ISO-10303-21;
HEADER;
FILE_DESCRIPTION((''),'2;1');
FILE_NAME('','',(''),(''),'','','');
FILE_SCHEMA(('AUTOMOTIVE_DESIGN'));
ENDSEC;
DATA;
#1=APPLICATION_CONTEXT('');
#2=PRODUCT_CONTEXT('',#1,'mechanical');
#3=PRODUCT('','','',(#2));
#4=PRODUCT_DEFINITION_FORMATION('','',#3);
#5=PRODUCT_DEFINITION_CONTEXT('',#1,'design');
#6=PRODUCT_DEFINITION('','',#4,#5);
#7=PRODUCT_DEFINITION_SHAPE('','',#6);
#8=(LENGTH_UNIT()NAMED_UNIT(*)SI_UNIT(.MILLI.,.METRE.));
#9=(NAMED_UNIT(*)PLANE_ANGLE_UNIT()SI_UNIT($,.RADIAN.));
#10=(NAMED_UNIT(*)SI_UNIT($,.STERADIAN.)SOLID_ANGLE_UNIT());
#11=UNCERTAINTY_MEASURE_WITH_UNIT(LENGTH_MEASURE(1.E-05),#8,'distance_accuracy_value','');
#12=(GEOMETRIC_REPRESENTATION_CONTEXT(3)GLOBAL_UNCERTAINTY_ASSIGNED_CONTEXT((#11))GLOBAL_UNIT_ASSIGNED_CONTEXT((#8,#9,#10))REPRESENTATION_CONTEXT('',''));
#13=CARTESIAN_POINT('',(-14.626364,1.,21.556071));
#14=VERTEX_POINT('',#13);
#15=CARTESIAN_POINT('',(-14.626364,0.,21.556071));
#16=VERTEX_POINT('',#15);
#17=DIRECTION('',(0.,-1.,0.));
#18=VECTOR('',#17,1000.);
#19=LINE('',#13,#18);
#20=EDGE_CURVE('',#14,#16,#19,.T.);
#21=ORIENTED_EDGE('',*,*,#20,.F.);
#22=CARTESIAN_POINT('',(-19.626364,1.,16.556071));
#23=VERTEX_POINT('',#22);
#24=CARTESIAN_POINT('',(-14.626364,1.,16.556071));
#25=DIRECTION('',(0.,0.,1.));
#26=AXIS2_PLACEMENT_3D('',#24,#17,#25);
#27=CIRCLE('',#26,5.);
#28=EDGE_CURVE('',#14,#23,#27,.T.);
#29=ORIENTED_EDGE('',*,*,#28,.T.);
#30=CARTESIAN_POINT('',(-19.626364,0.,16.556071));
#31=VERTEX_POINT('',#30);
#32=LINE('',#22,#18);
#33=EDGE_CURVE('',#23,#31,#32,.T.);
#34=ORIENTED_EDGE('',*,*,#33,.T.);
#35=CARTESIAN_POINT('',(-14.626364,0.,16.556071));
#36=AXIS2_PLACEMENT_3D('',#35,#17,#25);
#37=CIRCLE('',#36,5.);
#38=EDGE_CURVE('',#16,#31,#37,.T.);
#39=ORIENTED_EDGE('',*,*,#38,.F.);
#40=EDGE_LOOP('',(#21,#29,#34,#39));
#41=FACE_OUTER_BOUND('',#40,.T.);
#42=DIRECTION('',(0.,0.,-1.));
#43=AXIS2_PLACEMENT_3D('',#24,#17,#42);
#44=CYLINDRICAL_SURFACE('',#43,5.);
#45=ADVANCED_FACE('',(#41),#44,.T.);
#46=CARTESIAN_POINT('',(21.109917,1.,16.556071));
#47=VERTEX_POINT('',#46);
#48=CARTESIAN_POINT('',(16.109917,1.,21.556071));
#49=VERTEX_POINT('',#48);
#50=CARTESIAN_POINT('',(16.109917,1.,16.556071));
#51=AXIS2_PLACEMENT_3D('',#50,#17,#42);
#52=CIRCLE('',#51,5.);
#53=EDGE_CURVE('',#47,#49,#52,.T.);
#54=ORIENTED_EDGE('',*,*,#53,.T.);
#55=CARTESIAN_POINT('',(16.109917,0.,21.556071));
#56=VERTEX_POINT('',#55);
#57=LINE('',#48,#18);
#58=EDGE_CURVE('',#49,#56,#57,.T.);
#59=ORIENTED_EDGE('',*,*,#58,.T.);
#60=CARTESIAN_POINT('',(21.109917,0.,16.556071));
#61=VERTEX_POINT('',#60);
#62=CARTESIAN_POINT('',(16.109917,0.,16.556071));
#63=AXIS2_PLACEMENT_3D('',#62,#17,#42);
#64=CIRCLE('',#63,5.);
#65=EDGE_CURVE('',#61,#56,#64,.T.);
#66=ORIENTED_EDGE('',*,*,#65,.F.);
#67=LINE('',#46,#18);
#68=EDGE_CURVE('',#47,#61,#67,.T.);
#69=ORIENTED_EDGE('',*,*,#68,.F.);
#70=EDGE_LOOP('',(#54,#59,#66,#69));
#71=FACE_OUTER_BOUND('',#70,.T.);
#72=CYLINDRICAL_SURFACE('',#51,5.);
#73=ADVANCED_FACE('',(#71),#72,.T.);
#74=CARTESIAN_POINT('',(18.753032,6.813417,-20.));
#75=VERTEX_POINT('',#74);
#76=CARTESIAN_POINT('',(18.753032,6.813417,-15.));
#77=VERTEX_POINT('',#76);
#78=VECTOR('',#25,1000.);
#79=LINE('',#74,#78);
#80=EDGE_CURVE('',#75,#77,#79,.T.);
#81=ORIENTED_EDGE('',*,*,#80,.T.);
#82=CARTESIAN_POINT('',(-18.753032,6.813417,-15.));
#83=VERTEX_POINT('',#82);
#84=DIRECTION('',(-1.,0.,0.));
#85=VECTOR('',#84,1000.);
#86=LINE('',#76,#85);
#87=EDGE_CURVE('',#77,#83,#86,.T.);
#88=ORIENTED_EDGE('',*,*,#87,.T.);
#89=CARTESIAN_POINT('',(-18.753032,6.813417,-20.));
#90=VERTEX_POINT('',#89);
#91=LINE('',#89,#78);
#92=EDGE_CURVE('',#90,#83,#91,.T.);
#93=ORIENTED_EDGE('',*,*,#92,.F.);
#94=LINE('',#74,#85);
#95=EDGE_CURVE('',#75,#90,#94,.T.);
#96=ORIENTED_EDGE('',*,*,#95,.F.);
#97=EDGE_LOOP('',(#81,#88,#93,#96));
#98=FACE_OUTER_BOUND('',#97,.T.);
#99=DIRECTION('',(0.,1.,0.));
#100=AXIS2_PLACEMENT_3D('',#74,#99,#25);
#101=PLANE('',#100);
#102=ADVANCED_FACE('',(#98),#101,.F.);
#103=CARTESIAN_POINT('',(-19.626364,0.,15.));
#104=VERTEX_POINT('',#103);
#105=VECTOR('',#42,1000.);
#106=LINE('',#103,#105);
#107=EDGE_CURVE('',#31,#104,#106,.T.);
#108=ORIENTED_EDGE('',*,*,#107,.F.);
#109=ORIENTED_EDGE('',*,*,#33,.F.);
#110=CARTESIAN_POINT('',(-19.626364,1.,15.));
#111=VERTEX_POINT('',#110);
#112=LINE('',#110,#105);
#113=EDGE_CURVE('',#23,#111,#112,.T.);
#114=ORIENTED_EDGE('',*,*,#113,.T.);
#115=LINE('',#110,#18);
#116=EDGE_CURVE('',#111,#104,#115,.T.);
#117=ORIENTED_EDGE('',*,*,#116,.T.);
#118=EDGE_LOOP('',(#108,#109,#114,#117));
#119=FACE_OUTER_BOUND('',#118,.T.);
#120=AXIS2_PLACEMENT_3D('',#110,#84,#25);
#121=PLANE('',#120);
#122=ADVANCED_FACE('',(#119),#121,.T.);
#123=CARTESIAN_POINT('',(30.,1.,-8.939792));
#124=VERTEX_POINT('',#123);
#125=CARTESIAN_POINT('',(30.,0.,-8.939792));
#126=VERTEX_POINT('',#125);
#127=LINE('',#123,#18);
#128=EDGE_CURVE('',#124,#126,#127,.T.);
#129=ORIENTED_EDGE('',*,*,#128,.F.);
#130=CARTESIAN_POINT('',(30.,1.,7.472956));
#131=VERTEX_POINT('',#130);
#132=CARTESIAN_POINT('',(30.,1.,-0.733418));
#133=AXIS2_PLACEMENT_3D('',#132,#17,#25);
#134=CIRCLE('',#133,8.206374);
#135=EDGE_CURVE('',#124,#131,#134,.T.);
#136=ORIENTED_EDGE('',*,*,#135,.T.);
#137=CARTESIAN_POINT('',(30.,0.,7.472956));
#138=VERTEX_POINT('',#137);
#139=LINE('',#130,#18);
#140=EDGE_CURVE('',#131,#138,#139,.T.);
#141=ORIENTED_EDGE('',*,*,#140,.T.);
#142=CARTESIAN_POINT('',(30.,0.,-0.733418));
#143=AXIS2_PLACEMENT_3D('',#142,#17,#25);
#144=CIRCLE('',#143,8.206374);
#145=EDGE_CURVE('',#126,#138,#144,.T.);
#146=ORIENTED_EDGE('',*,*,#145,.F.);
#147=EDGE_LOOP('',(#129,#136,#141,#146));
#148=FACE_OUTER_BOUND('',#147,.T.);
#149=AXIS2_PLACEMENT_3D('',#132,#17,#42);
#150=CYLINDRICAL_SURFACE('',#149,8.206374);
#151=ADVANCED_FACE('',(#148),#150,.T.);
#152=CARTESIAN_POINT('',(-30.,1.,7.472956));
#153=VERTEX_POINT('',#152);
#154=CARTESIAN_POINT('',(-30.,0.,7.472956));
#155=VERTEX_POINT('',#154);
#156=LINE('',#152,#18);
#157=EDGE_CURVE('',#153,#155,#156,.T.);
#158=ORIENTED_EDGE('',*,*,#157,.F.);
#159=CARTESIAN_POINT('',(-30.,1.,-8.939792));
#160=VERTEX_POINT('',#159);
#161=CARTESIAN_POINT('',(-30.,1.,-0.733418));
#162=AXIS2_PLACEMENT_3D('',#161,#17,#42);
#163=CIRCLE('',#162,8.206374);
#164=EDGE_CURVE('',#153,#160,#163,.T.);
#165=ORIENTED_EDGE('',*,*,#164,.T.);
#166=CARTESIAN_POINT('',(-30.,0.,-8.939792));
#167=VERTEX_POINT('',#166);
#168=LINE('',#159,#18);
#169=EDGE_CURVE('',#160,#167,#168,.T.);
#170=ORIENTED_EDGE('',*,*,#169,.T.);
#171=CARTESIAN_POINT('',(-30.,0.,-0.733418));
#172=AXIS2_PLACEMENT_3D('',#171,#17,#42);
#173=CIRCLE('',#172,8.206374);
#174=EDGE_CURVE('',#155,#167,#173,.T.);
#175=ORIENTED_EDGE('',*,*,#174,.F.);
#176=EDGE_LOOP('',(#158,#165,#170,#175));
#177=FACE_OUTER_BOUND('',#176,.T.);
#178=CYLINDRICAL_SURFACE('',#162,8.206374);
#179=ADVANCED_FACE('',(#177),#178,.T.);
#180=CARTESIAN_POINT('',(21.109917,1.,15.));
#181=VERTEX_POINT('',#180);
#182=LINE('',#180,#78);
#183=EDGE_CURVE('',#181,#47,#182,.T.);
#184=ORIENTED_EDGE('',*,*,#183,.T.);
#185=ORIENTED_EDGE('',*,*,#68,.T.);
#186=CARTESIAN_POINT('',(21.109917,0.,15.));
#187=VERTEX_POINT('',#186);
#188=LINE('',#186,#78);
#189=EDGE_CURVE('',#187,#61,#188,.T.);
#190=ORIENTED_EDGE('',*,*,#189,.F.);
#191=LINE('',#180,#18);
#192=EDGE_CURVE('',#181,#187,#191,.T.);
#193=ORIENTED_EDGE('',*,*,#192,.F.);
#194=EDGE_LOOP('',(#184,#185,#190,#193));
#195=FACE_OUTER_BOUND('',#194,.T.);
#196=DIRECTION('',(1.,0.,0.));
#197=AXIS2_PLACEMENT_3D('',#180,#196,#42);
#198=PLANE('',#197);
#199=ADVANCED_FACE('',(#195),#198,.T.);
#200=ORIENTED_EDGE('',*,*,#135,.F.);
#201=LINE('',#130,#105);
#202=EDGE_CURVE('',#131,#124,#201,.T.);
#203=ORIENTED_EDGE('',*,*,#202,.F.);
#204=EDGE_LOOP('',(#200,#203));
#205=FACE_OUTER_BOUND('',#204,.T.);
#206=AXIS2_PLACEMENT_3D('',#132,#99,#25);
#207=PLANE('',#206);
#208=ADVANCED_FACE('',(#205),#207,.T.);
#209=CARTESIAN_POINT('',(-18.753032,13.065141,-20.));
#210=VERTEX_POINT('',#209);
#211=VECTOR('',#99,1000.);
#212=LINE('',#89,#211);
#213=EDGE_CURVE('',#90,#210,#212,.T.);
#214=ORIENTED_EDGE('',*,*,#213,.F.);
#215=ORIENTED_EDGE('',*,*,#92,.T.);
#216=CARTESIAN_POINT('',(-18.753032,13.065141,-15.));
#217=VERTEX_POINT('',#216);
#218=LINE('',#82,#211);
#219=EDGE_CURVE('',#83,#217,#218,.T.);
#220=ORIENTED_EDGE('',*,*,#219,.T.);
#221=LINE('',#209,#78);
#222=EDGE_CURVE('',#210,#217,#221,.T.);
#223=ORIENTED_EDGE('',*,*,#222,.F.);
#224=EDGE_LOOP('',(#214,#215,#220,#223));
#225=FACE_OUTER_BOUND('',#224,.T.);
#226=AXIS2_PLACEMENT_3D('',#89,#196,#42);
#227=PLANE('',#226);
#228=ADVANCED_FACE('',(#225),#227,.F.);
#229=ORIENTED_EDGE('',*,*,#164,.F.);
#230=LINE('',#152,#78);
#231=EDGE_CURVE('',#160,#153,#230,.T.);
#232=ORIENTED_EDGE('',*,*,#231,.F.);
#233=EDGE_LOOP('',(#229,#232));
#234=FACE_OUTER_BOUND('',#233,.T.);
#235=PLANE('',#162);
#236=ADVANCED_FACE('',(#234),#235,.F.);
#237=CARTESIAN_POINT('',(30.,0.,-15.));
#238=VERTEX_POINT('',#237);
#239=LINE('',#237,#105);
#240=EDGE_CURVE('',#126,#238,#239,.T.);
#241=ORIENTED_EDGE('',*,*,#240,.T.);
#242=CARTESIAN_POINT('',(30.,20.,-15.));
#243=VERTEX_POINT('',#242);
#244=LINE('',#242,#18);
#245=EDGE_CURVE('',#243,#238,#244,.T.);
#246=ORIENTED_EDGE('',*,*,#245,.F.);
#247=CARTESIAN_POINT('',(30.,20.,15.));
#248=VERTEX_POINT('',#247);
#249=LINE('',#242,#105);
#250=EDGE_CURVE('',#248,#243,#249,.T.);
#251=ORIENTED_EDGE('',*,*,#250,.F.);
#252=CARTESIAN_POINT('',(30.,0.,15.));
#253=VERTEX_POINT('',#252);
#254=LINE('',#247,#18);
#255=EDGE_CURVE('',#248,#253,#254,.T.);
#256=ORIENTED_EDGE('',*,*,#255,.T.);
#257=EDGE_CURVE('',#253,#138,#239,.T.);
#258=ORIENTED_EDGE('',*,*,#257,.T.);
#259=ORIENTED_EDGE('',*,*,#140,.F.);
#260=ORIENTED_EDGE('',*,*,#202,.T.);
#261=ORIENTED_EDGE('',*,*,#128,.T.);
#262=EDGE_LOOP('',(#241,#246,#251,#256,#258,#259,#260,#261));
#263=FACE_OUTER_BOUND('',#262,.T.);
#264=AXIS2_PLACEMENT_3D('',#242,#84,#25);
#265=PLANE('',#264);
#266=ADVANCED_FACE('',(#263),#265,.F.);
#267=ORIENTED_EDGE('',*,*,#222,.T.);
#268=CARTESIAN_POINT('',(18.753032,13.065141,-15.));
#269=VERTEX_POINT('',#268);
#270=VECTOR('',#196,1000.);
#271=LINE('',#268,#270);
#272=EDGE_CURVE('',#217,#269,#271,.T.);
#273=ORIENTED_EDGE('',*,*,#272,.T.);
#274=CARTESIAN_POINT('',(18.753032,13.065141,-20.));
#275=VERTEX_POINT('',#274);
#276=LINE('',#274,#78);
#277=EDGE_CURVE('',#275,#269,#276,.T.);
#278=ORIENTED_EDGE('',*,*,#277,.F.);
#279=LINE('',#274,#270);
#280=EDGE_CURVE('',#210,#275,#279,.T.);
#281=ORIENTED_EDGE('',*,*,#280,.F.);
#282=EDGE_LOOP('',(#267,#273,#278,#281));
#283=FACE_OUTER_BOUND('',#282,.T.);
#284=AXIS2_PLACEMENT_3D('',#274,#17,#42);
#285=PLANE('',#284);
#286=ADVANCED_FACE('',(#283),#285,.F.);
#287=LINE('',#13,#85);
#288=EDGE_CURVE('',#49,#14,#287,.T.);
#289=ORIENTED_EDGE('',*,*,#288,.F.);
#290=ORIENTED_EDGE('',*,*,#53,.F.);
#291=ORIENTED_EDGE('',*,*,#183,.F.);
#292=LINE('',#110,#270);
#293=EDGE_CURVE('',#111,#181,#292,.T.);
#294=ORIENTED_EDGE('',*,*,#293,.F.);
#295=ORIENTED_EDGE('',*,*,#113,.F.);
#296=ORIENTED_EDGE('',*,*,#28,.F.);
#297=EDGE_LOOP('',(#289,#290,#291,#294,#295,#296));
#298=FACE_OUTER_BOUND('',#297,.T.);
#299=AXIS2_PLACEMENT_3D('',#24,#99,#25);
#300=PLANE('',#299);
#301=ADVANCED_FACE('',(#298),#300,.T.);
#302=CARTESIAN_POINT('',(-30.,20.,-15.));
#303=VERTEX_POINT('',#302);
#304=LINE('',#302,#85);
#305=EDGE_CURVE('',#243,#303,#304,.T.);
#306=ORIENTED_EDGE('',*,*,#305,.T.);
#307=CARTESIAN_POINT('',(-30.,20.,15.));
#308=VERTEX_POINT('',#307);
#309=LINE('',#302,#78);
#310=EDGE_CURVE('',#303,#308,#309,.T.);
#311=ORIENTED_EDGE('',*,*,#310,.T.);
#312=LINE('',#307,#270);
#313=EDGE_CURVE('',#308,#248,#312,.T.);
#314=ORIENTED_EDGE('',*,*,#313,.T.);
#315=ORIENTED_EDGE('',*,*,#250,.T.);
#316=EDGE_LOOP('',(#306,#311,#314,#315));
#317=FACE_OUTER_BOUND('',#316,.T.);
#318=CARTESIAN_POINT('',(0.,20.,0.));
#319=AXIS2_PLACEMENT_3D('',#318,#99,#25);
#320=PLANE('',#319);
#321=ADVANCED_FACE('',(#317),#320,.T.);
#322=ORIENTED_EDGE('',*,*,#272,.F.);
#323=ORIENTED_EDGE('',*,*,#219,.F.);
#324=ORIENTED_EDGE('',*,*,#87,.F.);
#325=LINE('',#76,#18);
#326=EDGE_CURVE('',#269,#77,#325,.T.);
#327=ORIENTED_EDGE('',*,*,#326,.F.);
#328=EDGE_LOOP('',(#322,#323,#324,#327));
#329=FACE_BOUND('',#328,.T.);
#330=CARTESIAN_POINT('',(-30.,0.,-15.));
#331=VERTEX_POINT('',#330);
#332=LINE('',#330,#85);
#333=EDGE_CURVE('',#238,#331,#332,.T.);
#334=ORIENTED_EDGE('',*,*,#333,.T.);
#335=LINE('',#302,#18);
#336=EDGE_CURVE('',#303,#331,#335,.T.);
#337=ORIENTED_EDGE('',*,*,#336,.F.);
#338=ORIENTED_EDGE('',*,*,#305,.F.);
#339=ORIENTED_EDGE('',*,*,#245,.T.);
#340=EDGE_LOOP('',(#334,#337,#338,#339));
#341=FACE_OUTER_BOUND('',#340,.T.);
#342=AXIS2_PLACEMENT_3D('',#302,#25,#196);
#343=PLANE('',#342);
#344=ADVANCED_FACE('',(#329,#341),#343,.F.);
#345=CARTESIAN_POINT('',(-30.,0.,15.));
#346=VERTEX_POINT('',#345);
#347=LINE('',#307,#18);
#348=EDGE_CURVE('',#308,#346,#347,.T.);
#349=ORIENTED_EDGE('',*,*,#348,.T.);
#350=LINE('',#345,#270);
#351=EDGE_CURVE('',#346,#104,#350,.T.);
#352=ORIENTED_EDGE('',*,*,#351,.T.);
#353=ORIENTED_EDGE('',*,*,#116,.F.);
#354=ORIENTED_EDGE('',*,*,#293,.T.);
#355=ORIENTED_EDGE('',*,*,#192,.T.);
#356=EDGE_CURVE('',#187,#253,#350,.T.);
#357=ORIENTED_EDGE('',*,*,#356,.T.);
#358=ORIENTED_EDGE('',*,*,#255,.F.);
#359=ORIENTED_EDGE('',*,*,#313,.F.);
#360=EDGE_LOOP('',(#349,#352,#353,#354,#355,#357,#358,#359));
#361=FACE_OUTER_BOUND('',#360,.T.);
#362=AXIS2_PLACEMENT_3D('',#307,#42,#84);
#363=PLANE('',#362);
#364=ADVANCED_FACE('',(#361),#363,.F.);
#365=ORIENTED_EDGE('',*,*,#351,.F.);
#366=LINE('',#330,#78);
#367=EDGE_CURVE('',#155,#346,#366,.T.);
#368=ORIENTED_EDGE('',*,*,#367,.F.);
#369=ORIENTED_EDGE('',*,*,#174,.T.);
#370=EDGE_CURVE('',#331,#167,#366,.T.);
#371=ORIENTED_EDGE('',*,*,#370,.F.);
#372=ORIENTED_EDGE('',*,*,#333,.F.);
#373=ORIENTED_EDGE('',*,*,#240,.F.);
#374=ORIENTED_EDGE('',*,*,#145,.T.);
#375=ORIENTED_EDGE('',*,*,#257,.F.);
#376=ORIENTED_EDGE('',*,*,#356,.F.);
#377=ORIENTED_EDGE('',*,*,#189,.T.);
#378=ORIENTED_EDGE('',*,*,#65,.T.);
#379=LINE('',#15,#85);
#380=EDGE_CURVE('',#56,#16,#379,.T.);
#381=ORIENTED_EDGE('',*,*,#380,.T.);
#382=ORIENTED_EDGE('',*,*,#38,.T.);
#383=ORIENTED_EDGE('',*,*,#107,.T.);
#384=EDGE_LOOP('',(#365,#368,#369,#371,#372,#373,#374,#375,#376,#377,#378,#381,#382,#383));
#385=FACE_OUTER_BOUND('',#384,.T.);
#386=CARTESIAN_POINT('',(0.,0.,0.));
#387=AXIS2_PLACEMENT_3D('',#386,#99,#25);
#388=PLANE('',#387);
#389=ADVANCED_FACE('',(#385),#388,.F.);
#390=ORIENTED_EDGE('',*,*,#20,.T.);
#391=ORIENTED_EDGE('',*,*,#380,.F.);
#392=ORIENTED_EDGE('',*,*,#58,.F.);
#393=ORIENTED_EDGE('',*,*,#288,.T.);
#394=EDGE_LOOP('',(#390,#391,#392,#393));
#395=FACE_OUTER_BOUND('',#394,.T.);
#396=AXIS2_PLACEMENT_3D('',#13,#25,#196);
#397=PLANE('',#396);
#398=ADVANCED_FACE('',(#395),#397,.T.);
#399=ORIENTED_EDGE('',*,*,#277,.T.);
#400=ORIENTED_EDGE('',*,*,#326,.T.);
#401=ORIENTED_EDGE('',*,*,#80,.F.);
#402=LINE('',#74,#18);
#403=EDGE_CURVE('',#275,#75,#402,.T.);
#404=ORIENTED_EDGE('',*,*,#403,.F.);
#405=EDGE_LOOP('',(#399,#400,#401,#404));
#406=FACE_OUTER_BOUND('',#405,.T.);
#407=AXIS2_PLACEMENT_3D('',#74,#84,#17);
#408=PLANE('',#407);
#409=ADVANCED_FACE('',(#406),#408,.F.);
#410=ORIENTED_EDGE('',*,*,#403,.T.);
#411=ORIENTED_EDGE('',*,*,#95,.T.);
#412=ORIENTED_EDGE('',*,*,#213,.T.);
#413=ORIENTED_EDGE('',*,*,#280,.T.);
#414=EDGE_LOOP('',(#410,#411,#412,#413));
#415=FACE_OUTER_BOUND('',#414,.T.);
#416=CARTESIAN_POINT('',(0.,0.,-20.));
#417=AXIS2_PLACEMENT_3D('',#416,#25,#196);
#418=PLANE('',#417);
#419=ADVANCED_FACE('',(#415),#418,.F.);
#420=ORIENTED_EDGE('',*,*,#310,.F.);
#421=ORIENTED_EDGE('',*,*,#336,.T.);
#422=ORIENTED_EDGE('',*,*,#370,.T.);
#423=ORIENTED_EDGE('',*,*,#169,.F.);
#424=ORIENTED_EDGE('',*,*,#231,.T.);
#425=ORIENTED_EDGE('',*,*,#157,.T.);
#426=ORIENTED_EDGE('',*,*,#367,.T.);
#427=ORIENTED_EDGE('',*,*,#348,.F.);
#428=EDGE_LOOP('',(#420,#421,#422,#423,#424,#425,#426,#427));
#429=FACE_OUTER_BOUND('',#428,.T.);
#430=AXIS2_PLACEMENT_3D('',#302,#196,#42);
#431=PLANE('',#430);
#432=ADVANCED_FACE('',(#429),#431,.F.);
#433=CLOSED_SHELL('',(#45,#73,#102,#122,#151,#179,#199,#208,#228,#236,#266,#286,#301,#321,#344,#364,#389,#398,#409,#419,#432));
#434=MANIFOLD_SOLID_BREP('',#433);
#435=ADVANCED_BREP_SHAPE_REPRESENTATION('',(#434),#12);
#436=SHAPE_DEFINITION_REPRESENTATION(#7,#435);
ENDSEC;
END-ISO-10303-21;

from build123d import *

# Parameters (mm, degrees)
SKETCH1_W           = 60
SKETCH1_H           = 30
BOSS_EXTRUDE1_DEPTH = 20
SKETCH2_W           = 37.506064646
SKETCH2_H           = 6.251724505
BOSS_EXTRUDE2_DEPTH = 5
BOSS_EXTRUDE3_DEPTH = 1


with BuildPart() as part:
    # Sketch1 → Boss-Extrude1 (new body)
    with BuildSketch(Plane(origin=(0, 0, 0), x_dir=(1, 0, 0), z_dir=(0, 1, 0))):
        Rectangle(SKETCH1_W, SKETCH1_H)
    extrude(amount=BOSS_EXTRUDE1_DEPTH)

    # Sketch2 → Boss-Extrude2 (add)
    with BuildSketch(Plane(origin=(0, 0, -15), x_dir=(-1, 0, 0), z_dir=(0, 0, -1))):
        with Locations((0, 9.939278845)):
            Rectangle(SKETCH2_W, SKETCH2_H)
    extrude(amount=BOSS_EXTRUDE2_DEPTH)

    # Sketch3 → Boss-Extrude3 (add)
    with BuildSketch(Plane.XZ):
        with BuildLine():
            Line((-30, 7.472956379), (-30, -8.939791774))
            ThreePointArc((-30, -8.939791774), (-38.206374076, -0.733417697), (-30, 7.472956379))
        make_face()
        with BuildLine():
            Line((30, 7.472956379), (30, -8.939791774))
            ThreePointArc((30, -8.939791774), (38.206374076, -0.733417697), (30, 7.472956379))
        make_face()
        with BuildLine():
            Line((-19.626363832, 15), (21.109917151, 15))
            Line((21.109917151, 15), (21.109917151, 16.556070662))
            ThreePointArc((21.109917151, 16.556070662), (19.645451057, 20.091604568), (16.109917151, 21.556070662))
            Line((16.109917151, 21.556070662), (-14.626363832, 21.556070662))
            ThreePointArc((-14.626363832, 21.556070662), (-18.161897738, 20.091604568), (-19.626363832, 16.556070662))
            Line((-19.626363832, 16.556070662), (-19.626363832, 15))
        make_face()
    extrude(amount=-BOSS_EXTRUDE3_DEPTH)


solid = part.part
